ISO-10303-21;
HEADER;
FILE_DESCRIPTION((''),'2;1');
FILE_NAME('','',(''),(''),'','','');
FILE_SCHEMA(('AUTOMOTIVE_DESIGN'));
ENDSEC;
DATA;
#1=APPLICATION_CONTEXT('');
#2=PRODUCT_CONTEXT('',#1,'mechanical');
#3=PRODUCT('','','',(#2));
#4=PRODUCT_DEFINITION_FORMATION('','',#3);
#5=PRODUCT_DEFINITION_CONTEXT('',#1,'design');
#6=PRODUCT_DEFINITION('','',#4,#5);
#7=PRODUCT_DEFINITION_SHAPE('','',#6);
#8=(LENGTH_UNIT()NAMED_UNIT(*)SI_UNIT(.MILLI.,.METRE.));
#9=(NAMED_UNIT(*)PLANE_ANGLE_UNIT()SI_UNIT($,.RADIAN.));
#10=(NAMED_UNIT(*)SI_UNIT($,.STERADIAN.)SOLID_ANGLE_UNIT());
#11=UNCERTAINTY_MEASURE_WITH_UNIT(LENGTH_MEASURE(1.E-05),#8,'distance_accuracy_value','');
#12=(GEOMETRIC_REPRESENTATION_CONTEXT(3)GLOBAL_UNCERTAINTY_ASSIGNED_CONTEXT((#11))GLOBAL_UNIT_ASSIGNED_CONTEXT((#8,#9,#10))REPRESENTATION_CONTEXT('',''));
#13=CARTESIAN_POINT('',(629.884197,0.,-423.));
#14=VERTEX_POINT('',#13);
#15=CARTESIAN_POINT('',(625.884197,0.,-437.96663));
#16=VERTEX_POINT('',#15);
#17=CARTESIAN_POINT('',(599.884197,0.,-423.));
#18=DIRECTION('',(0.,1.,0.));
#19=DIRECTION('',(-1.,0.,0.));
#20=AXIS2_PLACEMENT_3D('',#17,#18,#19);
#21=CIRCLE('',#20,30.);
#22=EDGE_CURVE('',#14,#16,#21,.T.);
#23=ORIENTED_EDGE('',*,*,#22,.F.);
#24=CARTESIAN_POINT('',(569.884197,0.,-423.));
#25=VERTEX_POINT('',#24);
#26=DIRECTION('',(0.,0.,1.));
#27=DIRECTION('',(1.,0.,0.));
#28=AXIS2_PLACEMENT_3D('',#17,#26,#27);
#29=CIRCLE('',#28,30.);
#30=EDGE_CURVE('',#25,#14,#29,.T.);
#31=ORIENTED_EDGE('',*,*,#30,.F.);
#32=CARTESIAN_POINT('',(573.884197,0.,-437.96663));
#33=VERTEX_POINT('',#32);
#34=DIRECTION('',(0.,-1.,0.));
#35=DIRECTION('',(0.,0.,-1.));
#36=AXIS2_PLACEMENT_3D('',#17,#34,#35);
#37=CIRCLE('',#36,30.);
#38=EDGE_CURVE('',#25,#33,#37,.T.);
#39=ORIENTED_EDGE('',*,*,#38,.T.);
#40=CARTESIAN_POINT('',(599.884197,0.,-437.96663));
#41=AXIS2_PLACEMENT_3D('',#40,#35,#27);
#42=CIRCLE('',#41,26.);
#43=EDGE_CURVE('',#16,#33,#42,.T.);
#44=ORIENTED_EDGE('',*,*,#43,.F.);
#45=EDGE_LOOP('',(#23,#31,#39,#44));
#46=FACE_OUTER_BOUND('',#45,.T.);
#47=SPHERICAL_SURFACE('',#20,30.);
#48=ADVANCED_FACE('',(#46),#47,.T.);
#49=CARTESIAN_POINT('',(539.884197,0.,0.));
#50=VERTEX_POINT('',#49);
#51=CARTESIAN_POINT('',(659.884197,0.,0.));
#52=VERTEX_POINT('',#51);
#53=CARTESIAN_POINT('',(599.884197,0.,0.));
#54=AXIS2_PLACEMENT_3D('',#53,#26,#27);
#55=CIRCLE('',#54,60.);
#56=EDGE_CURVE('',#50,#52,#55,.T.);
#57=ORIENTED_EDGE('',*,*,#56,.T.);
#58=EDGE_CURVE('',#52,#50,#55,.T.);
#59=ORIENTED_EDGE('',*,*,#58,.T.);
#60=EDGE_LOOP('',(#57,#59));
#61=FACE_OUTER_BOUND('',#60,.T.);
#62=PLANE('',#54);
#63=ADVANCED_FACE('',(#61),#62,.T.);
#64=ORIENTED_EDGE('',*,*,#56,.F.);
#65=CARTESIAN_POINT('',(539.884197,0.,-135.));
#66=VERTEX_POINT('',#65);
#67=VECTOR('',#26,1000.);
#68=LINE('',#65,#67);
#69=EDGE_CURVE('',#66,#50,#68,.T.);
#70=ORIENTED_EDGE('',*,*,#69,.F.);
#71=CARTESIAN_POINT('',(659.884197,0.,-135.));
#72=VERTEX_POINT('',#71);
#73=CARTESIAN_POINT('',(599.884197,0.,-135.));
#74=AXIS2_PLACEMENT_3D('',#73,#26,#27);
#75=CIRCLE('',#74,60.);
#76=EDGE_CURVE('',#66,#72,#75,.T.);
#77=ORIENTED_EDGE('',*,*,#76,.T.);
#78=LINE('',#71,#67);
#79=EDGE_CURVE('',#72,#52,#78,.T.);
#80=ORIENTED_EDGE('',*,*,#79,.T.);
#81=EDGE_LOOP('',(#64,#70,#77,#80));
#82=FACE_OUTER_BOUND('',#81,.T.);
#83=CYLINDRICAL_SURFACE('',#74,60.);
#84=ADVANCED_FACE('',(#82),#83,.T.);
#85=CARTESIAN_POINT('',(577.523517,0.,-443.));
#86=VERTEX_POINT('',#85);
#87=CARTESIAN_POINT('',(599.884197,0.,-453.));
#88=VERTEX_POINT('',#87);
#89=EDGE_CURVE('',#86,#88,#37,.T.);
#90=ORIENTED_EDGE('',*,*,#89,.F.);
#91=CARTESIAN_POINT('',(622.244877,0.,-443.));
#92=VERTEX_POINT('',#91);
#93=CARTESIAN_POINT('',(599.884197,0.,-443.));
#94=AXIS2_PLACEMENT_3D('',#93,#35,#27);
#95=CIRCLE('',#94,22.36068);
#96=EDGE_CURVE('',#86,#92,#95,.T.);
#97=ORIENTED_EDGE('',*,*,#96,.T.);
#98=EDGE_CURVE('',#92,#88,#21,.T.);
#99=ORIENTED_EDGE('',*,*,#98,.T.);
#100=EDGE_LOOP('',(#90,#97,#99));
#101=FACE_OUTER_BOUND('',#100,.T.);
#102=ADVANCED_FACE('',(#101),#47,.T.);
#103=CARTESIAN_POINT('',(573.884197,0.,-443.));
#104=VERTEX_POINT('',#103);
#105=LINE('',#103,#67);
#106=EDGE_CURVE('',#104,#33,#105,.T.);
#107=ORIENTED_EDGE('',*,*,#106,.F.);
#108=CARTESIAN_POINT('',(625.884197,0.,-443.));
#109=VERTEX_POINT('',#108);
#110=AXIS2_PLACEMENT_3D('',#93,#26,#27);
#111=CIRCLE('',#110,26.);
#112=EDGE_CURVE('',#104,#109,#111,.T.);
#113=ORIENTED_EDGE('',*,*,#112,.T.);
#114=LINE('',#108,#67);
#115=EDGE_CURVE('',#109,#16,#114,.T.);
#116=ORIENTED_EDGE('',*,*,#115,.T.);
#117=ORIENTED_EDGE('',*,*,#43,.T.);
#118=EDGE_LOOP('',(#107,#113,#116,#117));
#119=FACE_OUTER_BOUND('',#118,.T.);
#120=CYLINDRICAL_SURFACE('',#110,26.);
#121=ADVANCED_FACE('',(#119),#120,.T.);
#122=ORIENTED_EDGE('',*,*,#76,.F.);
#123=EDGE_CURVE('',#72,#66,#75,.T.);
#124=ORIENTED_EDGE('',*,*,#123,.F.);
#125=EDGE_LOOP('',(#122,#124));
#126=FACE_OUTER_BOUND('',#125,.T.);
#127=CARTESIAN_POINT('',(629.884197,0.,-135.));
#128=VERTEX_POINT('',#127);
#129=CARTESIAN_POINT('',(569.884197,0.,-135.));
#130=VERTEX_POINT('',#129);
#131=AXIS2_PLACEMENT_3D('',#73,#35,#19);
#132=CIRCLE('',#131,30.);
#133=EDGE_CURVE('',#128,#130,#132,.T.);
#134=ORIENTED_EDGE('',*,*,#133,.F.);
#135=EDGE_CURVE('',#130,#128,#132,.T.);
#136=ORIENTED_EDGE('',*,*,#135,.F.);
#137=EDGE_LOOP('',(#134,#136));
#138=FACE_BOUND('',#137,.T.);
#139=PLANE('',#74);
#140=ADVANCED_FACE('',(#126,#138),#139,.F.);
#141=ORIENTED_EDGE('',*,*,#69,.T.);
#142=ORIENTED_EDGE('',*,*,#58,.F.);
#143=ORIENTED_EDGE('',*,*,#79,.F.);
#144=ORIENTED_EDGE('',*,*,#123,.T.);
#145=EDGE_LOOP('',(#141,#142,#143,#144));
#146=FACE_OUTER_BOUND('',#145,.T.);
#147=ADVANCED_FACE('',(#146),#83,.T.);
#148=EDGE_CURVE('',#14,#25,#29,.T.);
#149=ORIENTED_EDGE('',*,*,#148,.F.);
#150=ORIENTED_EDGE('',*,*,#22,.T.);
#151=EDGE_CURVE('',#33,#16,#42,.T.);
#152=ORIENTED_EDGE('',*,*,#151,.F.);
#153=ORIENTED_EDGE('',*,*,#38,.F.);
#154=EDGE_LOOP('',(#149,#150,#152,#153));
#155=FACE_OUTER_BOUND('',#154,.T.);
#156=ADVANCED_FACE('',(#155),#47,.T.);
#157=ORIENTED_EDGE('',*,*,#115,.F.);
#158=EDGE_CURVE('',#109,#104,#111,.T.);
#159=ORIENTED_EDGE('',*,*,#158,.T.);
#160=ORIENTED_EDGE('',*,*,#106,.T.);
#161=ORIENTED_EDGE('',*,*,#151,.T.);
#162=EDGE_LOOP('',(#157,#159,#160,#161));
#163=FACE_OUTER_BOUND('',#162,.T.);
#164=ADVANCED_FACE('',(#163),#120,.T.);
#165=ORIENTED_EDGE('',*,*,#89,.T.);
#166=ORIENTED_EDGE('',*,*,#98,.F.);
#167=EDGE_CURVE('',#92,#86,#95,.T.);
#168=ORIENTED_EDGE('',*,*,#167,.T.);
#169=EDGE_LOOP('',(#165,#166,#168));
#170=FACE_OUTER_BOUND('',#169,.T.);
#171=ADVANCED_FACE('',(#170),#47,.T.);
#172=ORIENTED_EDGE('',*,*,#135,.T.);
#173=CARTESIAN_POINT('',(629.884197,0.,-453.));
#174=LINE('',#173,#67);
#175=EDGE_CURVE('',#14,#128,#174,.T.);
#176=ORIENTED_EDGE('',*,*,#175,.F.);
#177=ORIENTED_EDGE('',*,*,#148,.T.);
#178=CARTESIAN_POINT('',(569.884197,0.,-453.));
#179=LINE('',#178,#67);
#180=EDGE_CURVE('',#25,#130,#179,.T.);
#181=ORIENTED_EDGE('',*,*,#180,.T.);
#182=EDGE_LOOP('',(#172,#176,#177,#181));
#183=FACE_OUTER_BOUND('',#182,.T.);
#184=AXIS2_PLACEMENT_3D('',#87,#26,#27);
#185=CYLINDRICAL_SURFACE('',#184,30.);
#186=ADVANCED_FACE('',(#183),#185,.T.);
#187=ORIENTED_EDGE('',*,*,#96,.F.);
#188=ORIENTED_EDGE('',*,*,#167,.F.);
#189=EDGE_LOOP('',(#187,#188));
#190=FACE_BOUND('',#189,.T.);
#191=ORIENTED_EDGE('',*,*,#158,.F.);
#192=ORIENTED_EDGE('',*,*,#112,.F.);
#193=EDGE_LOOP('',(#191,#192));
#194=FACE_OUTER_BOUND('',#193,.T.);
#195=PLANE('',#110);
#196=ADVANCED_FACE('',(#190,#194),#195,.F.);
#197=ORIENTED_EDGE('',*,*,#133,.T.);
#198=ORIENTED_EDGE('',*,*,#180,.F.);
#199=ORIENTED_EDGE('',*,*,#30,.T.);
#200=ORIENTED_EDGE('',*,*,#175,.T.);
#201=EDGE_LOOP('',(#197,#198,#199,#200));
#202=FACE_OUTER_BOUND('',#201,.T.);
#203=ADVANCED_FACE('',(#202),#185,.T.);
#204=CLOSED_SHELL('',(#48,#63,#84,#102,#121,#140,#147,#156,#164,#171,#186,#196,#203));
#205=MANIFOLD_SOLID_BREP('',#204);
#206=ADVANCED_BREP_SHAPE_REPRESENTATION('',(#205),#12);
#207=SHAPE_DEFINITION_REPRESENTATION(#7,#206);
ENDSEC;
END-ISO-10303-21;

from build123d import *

# Parameters (mm, degrees)
SKETCH1_R           = 60
BOSS_EXTRUDE1_DEPTH = 135
SKETCH2_R           = 30
BOSS_EXTRUDE2_DEPTH = 318
FILLET2_R           = 30
SKETCH3_R           = 26
BOSS_EXTRUDE3_DEPTH = 20


with BuildPart() as part:
    # Sketch1 → Boss-Extrude1 (new body)
    with BuildSketch(Plane.XY):
        with Locations((599.884196758, 0)):
            Circle(SKETCH1_R)
    extrude(amount=-BOSS_EXTRUDE1_DEPTH)

    # Sketch2 → Boss-Extrude2 (add)
    with BuildSketch(Plane(origin=(0, 0, -135), x_dir=(-1, 0, 0), z_dir=(0, 0, -1))):
        with Locations((-599.884196758, 0)):
            Circle(SKETCH2_R)
    extrude(amount=BOSS_EXTRUDE2_DEPTH)

    # Fillet2
    fillet2_edges = [part.edges().sort_by_distance(p)[0] for p in [
        (629.884196758, 0, -453),
    ]]
    fillet(fillet2_edges, radius=FILLET2_R)

    # Sketch3 → Boss-Extrude3 (add)
    with BuildSketch(Plane.XY.offset(-423)):
        with Locations((599.884196758, 0)):
            Circle(SKETCH3_R)
    extrude(amount=-BOSS_EXTRUDE3_DEPTH)


solid = part.part
